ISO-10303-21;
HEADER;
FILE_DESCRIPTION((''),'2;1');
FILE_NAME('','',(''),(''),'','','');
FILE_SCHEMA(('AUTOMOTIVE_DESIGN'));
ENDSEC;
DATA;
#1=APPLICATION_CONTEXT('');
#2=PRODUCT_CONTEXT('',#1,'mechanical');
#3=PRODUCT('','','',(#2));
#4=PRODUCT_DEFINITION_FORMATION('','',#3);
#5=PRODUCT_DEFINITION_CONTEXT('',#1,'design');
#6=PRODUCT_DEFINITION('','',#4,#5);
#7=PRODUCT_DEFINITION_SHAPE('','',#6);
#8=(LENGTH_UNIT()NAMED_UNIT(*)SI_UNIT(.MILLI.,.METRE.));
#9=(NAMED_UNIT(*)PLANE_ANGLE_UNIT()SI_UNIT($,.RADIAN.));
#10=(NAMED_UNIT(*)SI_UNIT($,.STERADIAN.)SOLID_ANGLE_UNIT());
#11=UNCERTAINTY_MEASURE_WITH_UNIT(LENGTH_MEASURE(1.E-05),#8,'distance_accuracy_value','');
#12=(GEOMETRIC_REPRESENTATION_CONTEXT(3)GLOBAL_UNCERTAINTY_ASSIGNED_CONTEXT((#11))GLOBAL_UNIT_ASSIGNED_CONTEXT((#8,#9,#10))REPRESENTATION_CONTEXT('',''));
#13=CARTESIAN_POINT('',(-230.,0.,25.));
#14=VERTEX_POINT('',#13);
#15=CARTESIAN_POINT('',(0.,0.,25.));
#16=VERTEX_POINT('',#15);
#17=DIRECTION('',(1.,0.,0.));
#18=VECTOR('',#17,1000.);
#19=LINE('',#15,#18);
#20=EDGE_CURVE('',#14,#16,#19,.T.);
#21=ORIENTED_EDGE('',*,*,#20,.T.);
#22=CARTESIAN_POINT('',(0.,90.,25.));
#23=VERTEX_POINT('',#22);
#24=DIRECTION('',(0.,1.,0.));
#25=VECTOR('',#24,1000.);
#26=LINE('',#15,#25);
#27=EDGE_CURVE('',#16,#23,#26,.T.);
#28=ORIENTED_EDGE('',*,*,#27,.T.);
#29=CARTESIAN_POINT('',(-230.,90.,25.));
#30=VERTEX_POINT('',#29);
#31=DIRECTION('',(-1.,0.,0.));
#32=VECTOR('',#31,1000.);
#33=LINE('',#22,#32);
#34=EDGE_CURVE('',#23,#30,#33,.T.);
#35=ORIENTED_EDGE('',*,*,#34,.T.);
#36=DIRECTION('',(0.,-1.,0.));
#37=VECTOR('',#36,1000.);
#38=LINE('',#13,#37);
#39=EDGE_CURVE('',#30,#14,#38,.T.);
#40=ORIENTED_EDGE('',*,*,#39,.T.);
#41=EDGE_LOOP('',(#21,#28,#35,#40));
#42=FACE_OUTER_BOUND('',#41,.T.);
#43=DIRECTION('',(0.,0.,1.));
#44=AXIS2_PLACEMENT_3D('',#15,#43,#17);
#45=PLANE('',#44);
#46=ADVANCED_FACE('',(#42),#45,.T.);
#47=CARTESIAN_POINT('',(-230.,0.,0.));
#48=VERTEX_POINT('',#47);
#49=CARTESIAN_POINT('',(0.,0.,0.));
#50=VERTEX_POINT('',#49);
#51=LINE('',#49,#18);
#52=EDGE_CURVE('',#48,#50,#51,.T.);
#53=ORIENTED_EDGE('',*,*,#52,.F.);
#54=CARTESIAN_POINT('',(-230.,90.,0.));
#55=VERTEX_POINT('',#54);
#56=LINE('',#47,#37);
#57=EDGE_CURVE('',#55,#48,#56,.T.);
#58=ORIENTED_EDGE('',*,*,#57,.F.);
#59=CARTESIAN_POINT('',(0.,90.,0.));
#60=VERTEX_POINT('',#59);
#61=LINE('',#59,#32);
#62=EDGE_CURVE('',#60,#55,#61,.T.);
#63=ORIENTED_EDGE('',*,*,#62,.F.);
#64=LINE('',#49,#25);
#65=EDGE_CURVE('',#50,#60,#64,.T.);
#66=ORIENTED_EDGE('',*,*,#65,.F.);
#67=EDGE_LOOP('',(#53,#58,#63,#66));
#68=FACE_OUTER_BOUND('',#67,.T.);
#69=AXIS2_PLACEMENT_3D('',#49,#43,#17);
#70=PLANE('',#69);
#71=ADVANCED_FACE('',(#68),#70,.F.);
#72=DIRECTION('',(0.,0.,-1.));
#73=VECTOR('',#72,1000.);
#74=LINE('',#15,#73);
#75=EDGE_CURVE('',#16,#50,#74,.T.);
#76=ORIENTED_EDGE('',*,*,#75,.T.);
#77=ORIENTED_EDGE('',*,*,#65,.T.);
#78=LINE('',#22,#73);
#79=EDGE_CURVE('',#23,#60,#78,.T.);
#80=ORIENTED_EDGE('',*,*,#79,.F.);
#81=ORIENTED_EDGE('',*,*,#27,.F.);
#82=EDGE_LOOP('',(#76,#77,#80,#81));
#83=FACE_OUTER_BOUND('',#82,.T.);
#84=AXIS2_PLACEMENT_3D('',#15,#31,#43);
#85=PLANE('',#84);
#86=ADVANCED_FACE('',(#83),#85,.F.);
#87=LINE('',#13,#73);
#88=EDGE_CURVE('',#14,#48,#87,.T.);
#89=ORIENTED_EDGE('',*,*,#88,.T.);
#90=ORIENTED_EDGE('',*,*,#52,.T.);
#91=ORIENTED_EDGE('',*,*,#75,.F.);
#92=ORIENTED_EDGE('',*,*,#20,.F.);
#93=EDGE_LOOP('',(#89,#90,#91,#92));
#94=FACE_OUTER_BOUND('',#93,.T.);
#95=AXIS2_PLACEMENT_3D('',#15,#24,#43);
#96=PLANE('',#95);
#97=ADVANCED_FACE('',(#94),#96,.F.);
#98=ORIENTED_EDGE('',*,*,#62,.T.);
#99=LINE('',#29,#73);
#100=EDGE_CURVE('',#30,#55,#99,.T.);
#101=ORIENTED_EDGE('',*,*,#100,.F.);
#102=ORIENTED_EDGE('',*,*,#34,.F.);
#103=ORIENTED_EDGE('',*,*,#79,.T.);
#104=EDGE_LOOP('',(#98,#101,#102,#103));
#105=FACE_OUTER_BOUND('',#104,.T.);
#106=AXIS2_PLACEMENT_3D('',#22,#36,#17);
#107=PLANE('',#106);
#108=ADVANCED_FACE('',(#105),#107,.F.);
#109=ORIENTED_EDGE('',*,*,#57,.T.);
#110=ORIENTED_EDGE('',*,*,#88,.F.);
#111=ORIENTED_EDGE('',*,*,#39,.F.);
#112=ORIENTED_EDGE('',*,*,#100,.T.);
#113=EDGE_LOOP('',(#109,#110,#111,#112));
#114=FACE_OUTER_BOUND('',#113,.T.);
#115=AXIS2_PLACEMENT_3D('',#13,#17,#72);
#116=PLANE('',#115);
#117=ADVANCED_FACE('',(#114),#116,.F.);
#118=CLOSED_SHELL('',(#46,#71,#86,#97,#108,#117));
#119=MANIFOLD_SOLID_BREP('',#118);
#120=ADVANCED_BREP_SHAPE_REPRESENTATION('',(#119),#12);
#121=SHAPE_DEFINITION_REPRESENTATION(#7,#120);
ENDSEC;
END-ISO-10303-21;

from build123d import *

# Parameters (mm, degrees)
SKETCH1_W           = 230
SKETCH1_H           = 90
BOSS_EXTRUDE1_DEPTH = 25


with BuildPart() as part:
    # Sketch1 → Boss-Extrude1 (new body)
    with BuildSketch(Plane.XY):
        with Locations((-115, 45)):
            Rectangle(SKETCH1_W, SKETCH1_H)
    extrude(amount=BOSS_EXTRUDE1_DEPTH)


solid = part.part
